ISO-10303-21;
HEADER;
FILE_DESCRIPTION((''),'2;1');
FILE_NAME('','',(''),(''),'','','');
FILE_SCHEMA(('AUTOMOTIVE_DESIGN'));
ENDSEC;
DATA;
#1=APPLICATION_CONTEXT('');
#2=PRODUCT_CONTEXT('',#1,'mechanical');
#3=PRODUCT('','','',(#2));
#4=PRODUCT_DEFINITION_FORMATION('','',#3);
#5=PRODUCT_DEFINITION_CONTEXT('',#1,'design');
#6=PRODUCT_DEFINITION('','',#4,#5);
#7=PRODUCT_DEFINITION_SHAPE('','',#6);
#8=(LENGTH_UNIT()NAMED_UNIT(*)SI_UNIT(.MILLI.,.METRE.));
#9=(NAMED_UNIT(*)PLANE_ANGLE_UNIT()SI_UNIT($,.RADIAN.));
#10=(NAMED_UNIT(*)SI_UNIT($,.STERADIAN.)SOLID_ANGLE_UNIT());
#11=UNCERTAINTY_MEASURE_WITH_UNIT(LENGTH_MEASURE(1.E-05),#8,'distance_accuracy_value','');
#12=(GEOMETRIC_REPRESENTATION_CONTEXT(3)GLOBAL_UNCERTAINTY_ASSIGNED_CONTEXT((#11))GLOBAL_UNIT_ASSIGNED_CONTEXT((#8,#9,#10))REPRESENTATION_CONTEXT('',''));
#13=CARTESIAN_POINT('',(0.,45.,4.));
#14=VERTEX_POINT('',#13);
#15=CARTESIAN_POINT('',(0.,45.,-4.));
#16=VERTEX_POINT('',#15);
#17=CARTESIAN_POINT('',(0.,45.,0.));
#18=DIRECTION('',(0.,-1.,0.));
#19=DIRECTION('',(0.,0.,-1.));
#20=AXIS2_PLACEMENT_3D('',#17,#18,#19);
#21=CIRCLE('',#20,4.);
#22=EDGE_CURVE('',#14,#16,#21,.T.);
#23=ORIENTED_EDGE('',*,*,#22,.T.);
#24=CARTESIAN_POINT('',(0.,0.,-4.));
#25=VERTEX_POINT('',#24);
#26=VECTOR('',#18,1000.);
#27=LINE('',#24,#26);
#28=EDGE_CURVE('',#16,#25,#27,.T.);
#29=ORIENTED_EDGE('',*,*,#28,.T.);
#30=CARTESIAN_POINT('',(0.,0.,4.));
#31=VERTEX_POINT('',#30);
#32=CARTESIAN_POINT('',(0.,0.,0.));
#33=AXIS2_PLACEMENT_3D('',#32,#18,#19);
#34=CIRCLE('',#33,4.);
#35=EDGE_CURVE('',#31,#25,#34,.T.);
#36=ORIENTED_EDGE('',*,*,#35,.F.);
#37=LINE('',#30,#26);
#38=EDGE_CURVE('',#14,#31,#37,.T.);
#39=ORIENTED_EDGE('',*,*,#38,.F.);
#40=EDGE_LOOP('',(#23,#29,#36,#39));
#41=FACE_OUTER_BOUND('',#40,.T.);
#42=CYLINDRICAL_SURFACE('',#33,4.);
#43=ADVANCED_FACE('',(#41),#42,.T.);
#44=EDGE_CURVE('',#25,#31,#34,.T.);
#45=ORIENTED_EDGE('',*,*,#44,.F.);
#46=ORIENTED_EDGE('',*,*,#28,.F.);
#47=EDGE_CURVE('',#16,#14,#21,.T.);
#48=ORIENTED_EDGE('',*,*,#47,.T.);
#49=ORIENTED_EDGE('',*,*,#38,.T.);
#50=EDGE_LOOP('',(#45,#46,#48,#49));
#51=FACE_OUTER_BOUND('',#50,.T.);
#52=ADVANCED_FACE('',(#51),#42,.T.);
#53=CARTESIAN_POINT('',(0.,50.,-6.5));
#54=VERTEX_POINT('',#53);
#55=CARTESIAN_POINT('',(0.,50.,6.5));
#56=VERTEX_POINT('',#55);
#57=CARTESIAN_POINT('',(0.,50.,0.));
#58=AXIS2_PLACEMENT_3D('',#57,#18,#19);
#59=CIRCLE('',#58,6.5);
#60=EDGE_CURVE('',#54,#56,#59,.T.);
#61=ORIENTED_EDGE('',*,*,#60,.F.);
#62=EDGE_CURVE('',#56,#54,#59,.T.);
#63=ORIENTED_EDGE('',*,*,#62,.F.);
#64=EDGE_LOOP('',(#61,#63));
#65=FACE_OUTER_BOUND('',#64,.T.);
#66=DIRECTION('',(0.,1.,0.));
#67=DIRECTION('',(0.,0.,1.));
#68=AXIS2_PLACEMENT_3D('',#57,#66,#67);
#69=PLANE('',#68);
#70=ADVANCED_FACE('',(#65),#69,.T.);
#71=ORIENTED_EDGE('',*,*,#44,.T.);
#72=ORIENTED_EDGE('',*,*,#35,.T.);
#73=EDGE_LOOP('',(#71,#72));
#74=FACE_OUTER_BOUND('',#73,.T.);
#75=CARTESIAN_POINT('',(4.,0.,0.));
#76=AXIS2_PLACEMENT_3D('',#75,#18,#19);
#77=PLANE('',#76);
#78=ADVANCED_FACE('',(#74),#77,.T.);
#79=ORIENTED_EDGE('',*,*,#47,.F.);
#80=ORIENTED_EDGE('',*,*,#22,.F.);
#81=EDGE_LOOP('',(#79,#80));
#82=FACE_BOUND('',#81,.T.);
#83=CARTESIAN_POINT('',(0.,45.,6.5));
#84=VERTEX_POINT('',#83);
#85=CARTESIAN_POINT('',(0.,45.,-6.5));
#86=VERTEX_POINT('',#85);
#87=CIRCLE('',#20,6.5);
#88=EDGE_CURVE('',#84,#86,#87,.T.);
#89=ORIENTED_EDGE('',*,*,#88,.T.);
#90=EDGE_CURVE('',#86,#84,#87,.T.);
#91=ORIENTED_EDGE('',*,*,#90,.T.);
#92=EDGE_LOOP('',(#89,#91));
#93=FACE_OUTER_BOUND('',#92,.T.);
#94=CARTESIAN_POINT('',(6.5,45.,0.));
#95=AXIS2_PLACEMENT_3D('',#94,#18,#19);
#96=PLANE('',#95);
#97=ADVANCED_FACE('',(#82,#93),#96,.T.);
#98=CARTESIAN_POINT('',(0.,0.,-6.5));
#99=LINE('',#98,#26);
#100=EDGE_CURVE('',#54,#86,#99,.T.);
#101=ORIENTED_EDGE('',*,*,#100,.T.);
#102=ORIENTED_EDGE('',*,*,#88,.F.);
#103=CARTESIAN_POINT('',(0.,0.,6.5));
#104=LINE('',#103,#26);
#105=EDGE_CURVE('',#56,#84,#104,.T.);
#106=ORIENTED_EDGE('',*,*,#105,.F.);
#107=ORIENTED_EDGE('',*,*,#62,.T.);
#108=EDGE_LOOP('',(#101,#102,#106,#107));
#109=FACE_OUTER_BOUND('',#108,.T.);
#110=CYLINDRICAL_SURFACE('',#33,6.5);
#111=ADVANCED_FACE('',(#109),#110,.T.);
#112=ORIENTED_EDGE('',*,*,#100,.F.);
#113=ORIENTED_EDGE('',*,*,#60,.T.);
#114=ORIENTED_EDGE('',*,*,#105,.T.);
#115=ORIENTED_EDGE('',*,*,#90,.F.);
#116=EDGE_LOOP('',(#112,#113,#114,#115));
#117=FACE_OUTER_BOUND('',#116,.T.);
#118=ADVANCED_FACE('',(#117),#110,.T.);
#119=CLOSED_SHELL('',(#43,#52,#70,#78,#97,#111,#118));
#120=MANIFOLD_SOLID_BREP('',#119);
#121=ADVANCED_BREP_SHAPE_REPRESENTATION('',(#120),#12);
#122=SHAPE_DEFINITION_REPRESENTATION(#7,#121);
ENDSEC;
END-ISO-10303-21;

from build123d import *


with BuildPart() as part:
    # Sketch1 → Revolve1 (revolve)
    with BuildSketch(Plane.XY, mode=Mode.PRIVATE) as revolve1_sk:
        Polygon((0, 0), (0, 50), (6.5, 50), (6.5, 45), (4, 45), (4, 0), align=None)
    revolve(revolve1_sk.sketch.rotate(Axis((0, 0, 0), (0, 1, 0)), 90), axis=Axis((0, 0, 0), (0, 1, 0)))


solid = part.part
